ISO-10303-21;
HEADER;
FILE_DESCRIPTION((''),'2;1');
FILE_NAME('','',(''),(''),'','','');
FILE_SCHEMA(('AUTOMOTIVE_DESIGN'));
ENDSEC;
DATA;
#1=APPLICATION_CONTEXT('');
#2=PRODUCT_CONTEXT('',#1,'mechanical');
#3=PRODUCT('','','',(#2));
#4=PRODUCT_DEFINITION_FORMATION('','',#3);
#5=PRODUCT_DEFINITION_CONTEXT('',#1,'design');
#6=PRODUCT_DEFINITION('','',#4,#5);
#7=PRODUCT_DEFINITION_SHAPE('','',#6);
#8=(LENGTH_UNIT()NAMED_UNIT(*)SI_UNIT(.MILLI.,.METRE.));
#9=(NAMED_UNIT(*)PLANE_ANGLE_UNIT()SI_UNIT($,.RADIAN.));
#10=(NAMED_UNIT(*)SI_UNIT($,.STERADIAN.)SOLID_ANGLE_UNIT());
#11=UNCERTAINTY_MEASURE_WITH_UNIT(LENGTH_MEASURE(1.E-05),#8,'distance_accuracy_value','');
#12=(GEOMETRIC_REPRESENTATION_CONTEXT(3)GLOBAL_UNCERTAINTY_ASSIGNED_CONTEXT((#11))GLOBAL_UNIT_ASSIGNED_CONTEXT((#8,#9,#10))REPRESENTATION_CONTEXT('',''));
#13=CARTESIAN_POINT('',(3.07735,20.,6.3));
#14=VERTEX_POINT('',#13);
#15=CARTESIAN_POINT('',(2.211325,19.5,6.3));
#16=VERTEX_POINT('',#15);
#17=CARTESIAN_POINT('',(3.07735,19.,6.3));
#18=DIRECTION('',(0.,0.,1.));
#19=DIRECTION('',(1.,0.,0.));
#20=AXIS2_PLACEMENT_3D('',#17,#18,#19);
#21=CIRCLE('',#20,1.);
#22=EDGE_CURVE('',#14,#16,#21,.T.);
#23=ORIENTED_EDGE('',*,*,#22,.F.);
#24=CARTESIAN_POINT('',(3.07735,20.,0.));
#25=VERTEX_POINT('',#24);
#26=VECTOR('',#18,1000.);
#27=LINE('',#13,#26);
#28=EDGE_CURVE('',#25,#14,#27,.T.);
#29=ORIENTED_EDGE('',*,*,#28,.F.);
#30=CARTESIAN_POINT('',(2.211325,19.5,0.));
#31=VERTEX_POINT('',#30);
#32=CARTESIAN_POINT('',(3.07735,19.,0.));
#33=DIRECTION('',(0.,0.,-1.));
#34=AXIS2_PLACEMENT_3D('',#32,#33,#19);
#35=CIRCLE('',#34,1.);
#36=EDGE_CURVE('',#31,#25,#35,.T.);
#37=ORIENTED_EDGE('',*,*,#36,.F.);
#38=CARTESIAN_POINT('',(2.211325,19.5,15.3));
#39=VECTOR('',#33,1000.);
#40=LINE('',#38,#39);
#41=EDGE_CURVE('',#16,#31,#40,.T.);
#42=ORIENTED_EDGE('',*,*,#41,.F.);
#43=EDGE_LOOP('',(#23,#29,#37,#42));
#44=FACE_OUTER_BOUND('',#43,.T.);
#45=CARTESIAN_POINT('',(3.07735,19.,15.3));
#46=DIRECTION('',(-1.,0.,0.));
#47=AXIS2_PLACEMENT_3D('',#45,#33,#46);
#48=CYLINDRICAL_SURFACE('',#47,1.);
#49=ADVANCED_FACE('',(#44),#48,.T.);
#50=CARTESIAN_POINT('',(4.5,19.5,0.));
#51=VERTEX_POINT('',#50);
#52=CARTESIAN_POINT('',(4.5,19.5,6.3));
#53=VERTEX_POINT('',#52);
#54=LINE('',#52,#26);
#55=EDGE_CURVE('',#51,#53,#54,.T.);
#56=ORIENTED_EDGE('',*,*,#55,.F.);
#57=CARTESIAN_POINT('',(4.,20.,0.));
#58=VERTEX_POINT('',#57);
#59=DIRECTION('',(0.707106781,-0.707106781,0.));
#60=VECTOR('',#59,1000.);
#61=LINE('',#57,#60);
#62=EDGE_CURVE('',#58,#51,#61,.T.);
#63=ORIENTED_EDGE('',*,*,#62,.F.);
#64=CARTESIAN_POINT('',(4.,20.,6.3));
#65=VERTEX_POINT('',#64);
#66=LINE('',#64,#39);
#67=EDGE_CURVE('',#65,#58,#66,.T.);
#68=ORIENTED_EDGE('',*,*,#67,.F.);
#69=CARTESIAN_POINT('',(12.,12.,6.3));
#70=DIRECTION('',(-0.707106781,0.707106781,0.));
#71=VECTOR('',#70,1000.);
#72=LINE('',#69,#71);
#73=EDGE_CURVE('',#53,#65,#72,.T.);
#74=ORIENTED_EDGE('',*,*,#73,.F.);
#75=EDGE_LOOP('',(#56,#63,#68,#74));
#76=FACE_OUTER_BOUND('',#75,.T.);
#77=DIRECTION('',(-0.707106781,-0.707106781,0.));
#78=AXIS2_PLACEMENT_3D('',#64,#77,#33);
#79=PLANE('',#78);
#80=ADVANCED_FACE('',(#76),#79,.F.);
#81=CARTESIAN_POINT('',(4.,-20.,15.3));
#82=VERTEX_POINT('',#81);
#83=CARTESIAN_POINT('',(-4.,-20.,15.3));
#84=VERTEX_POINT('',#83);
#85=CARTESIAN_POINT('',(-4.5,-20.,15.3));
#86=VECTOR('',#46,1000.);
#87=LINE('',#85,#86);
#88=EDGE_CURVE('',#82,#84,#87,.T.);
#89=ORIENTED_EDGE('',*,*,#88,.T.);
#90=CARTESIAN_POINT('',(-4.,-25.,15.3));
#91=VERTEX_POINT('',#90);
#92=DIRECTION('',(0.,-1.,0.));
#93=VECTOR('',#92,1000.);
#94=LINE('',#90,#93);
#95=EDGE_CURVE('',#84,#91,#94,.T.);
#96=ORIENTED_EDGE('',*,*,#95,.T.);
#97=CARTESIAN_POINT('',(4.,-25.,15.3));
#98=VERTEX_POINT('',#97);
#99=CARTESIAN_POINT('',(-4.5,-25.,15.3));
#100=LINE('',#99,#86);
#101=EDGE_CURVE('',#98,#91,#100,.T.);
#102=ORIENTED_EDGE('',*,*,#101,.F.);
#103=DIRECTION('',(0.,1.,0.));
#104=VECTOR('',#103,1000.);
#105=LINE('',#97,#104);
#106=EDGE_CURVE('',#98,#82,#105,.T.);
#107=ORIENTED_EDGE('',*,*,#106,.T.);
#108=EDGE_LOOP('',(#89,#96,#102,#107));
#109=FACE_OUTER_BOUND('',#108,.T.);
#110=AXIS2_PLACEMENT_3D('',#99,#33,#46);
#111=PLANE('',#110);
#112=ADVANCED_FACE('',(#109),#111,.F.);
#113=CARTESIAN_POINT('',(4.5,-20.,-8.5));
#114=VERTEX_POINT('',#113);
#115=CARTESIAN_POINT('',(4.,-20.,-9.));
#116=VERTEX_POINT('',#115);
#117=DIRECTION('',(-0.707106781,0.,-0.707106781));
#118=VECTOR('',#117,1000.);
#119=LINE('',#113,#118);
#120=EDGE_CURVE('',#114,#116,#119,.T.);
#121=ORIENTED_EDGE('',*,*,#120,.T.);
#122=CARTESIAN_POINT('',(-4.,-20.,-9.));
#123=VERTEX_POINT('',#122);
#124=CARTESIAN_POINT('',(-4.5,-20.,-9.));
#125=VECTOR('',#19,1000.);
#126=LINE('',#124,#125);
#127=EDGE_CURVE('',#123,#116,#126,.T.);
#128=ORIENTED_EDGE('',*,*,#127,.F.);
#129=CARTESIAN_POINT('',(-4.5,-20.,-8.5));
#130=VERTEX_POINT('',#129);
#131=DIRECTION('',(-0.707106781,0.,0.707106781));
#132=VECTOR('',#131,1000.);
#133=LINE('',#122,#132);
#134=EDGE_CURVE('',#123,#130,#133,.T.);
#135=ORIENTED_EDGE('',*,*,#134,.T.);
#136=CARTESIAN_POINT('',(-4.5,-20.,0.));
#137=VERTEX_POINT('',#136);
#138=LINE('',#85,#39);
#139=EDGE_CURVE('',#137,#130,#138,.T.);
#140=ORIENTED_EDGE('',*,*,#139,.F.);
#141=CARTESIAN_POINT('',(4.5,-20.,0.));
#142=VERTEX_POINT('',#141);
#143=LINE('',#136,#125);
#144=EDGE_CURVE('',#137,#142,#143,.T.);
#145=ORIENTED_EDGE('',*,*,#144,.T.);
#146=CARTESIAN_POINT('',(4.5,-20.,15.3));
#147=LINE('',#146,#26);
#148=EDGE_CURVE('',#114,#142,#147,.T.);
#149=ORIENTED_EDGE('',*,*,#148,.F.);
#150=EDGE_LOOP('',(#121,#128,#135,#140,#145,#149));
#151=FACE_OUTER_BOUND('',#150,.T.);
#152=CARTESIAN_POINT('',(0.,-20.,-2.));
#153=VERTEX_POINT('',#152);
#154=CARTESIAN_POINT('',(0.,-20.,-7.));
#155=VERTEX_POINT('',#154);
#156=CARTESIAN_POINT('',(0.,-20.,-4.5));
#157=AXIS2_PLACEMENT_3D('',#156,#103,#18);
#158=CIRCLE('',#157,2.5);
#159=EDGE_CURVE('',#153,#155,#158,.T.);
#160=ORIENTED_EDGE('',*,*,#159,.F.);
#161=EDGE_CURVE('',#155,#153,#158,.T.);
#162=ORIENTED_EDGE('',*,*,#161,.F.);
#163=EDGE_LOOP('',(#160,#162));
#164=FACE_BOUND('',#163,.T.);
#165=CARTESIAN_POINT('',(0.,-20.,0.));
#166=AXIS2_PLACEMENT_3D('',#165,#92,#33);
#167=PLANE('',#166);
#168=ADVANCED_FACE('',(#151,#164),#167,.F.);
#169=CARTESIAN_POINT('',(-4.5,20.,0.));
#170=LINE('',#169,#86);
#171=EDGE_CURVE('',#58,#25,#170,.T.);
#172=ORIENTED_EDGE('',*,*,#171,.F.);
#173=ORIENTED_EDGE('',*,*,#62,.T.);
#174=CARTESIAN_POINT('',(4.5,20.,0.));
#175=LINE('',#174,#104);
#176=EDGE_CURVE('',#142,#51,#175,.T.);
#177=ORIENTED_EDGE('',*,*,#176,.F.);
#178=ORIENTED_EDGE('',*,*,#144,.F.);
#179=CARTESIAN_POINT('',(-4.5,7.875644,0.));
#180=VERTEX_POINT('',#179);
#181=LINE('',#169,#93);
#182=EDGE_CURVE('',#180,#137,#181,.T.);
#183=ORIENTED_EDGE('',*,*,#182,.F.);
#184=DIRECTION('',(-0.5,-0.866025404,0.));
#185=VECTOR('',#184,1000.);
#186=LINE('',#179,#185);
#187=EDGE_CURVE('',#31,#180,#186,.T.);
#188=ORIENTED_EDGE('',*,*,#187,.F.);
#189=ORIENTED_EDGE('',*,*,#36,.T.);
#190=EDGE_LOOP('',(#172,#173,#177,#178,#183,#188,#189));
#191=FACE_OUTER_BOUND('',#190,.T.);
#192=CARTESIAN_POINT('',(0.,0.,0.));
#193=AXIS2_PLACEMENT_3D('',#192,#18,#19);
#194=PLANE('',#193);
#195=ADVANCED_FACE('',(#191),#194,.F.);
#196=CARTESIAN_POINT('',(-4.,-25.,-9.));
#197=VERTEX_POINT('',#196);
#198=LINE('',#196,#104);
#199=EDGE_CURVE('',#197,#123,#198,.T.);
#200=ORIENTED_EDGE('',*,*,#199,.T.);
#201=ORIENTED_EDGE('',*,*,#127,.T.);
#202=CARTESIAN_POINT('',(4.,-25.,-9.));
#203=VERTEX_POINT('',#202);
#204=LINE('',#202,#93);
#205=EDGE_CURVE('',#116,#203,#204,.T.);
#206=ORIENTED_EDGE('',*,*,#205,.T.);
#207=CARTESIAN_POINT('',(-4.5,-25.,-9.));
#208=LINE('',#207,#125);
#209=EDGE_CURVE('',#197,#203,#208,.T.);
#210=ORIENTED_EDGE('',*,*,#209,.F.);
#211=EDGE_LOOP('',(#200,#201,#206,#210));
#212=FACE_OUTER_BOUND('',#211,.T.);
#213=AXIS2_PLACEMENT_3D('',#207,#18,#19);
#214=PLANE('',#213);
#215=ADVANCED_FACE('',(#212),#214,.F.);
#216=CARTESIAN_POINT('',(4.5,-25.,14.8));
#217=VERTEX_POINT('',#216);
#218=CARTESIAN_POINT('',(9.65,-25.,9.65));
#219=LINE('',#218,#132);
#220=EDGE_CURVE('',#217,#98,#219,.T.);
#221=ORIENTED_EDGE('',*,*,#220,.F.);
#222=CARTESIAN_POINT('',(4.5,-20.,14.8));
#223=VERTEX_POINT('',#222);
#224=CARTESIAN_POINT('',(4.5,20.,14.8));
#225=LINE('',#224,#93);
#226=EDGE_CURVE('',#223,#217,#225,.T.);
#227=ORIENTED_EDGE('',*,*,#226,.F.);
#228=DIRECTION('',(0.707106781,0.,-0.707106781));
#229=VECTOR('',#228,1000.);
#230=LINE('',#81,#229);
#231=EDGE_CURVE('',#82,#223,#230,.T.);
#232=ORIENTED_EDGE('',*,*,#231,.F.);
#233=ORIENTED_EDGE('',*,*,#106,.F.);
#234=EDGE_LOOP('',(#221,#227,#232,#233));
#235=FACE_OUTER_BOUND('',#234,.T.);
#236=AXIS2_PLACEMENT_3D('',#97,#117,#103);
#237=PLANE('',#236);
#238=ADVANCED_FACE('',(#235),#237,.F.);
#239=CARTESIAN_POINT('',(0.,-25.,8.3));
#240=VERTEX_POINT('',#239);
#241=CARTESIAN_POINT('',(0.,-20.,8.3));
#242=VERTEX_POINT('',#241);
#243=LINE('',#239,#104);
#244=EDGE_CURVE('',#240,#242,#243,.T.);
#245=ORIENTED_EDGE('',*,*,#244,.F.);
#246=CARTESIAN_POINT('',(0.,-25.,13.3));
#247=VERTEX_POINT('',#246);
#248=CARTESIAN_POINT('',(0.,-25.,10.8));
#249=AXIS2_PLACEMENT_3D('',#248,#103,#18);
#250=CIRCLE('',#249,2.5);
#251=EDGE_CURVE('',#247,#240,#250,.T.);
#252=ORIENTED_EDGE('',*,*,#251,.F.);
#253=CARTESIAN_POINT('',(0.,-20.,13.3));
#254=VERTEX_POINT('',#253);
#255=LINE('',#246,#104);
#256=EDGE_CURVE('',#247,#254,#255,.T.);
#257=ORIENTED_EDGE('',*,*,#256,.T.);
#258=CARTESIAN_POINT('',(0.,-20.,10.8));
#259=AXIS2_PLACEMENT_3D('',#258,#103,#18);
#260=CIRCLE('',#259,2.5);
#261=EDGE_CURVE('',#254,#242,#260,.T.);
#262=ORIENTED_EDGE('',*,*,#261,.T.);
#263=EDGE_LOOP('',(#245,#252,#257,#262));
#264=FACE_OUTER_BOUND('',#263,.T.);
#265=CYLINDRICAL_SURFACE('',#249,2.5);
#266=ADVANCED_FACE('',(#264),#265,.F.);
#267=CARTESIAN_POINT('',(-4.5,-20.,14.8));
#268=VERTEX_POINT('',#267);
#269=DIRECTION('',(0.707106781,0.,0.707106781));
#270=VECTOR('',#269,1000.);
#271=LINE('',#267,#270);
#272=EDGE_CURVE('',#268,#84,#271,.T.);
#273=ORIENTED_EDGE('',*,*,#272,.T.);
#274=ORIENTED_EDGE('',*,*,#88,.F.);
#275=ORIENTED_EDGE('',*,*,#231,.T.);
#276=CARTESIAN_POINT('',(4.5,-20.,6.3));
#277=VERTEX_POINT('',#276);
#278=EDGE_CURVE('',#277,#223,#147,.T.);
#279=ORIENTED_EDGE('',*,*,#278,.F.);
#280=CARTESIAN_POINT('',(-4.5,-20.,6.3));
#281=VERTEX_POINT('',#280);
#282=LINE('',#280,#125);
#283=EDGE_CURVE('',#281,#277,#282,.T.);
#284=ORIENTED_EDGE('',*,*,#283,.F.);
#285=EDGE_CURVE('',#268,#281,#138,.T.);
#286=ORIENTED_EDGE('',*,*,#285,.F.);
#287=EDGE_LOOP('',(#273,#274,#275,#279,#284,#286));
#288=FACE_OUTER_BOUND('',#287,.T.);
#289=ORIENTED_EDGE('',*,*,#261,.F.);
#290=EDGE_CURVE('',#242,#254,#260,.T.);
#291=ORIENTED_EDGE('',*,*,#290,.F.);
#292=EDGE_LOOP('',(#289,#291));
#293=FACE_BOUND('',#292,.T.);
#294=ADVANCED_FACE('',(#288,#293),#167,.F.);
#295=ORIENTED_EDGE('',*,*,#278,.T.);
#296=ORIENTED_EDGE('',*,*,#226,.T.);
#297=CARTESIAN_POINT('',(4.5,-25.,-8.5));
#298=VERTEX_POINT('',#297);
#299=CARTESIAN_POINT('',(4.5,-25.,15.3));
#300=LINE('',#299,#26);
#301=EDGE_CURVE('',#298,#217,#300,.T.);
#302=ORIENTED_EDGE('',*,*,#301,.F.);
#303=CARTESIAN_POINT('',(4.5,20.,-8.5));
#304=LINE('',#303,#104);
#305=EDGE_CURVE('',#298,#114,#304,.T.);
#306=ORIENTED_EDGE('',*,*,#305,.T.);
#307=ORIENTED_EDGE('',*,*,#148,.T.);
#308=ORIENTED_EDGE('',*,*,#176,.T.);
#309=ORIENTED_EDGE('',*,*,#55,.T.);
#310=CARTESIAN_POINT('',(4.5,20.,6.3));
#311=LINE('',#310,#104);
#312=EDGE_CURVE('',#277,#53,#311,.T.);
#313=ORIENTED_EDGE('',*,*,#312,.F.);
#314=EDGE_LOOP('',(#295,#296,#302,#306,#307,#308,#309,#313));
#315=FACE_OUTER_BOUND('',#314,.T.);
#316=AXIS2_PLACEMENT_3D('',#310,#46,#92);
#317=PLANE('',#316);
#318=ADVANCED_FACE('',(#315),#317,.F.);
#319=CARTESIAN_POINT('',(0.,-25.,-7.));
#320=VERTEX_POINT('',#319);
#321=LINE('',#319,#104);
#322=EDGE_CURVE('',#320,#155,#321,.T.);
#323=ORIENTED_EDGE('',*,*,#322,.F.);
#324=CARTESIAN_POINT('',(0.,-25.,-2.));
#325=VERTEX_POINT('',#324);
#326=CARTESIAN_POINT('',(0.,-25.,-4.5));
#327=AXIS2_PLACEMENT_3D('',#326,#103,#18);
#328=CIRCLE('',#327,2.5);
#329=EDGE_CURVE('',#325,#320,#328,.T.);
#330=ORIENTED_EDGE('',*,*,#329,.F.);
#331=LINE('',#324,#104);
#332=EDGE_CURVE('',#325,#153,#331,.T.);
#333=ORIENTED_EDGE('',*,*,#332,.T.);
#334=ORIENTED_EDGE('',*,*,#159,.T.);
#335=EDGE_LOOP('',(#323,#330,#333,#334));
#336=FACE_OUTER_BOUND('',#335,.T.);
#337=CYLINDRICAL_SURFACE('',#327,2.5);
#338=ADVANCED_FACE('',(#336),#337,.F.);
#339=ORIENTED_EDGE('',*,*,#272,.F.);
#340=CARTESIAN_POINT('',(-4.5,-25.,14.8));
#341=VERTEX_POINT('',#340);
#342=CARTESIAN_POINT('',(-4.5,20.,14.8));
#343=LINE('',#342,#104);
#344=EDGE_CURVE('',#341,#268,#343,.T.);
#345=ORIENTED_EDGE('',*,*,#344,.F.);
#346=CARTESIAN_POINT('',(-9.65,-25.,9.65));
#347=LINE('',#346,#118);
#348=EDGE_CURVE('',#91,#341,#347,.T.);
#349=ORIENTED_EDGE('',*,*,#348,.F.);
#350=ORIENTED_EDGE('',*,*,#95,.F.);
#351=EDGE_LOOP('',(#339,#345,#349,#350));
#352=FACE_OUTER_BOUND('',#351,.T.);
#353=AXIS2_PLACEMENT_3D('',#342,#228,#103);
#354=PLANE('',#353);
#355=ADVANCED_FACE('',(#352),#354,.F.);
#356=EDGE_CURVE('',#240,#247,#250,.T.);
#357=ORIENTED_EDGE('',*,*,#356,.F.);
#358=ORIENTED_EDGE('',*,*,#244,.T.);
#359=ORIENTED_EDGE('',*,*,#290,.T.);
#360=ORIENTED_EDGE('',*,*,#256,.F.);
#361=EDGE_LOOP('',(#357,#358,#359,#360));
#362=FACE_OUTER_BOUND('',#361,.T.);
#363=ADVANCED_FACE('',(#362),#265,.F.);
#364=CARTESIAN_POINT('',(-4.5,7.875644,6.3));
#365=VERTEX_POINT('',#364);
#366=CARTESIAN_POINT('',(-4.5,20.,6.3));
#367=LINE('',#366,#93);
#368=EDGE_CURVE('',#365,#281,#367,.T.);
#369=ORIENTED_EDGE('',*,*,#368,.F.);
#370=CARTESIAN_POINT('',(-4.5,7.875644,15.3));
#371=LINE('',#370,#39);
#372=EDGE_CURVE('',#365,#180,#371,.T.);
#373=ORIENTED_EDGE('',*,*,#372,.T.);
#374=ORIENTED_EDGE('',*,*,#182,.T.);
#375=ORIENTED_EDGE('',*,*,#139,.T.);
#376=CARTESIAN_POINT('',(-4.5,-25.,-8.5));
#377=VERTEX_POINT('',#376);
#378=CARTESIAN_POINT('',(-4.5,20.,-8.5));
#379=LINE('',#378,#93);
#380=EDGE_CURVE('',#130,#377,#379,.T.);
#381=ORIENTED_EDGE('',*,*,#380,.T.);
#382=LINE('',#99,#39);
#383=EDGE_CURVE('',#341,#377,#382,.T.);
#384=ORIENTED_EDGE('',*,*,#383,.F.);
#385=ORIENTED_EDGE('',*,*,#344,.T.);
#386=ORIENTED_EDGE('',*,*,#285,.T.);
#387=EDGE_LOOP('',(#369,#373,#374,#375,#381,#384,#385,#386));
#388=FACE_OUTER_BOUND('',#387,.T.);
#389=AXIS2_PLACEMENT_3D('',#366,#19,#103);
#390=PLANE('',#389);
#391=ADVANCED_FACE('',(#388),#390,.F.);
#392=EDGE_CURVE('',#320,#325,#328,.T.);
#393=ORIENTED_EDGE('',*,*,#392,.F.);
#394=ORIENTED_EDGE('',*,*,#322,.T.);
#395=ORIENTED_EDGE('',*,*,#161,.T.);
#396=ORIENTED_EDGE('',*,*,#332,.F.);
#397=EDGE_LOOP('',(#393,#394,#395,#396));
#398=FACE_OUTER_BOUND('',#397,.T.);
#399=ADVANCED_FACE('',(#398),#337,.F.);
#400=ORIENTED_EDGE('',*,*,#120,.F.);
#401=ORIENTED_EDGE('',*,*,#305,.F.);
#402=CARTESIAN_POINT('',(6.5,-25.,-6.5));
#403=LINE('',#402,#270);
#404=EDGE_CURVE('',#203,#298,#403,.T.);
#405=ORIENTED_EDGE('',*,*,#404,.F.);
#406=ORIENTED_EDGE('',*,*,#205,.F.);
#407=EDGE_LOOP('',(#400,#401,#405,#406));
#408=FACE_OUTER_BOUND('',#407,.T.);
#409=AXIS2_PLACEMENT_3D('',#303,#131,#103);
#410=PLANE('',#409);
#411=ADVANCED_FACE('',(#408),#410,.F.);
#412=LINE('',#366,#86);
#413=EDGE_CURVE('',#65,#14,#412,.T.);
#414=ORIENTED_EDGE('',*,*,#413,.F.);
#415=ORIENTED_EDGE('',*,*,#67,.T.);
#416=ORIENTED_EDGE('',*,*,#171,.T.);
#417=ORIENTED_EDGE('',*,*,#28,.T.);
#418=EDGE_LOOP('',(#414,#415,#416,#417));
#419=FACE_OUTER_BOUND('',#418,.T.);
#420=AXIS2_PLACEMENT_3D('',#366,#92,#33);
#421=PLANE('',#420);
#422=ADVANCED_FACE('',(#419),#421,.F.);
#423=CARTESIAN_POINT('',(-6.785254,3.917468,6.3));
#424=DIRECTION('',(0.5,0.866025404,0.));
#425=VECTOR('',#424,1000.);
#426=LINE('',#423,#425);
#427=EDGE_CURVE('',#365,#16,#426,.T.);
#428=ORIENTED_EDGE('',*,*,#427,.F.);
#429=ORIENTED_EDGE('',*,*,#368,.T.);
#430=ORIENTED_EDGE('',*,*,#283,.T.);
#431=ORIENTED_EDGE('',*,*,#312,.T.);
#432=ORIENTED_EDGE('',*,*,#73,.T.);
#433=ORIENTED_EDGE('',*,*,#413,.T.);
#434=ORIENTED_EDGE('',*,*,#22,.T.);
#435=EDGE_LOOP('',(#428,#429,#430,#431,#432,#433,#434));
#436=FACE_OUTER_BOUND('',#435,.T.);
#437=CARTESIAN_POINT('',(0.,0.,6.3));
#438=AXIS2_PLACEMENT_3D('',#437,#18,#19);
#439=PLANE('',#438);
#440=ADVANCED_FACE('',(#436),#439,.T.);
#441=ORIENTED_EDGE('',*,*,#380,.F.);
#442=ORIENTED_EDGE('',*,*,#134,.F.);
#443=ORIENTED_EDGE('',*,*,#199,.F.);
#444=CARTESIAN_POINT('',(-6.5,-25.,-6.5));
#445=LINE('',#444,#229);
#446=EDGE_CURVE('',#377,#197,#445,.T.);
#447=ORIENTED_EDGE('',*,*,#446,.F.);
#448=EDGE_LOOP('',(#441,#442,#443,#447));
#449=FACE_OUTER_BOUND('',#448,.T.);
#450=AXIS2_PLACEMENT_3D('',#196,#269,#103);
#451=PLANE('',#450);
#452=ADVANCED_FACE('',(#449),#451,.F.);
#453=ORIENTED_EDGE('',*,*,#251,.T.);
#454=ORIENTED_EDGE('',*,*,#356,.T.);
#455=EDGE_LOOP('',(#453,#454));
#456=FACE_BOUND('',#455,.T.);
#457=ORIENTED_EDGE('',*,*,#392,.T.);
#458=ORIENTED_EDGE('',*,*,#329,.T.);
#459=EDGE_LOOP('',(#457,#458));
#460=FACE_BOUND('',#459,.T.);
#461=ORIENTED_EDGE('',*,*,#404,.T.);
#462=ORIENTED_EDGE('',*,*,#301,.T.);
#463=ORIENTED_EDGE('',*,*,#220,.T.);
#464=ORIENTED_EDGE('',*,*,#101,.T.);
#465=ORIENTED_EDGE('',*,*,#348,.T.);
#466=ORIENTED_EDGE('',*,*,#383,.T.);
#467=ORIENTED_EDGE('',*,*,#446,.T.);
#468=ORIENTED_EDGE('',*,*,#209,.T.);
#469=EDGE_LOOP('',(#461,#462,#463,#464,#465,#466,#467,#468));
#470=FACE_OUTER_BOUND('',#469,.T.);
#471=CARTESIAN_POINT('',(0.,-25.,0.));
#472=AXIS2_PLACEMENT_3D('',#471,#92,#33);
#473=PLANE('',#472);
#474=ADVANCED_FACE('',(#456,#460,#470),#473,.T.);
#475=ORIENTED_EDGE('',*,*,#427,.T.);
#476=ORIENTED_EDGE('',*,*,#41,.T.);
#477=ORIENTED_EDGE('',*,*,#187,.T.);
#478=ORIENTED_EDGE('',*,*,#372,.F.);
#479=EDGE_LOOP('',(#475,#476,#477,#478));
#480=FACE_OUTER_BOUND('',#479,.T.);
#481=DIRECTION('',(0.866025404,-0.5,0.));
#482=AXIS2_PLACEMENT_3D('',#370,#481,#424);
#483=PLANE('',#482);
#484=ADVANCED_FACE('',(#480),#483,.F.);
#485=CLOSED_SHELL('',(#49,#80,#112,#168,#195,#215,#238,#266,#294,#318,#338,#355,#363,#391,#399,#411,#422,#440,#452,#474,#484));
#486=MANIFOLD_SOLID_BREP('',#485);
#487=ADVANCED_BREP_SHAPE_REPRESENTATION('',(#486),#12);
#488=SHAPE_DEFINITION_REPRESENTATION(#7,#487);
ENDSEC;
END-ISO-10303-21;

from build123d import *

# Parameters (mm, degrees)
SKETCH_1_W          = 9
SKETCH_1_H          = 40
EXTRUDE_1_DEPTH     = 6.3
SKETCH_2_W          = 9
SKETCH_2_H          = 24.3
EXTRUDE_2_DEPTH     = 5
CUT_EXTRUDE_1_DEPTH = 30.653667564
SKETCH_4_R          = 2.5
CUT_EXTRUDE_2_DEPTH = 44.062048256
FILLET_1_R          = 1
CHAMFER_2_SIZE      = 0.5


with BuildPart() as part:
    # 草图1 → 凸台-拉伸1 (new body)
    with BuildSketch(Plane.XY):
        Rectangle(SKETCH_1_W, SKETCH_1_H)
    extrude(amount=EXTRUDE_1_DEPTH)

    # 草图2 → 凸台-拉伸2 (add)
    with BuildSketch(Plane.XZ.offset(20)):
        with Locations((0, 3.15)):
            Rectangle(SKETCH_2_W, SKETCH_2_H)
    extrude(amount=EXTRUDE_2_DEPTH)

    # 草图3 → 切除-拉伸1 (cut, through all)
    with BuildSketch(Plane(origin=(0, 0, 0), x_dir=(-1, 0, 0), z_dir=(0, 0, -1))):
        Polygon((-2.5, 20), (4.5, 20), (4.5, 7.875644347), align=None)
    extrude(amount=-CUT_EXTRUDE_1_DEPTH, mode=Mode.SUBTRACT)

    # 草图4 → 切除-拉伸2 (cut, through all)
    with BuildSketch(Plane(origin=(0, -20, 0), x_dir=(1, 0, 0), z_dir=(0, 1, 0))):
        with Locations(Location((0, 4.5, 0), (0, 0, 270))):
            Circle(SKETCH_4_R)
        with Locations(Location((0, -10.8, 0), (0, 0, 270))):
            Circle(SKETCH_4_R)
    extrude(amount=-CUT_EXTRUDE_2_DEPTH, mode=Mode.SUBTRACT)

    # 圆角1
    fillet_1_edges = [part.edges().sort_by_distance(p)[0] for p in [
        (2.5, 20, 3.15),
    ]]
    fillet(fillet_1_edges, radius=FILLET_1_R)

    # 倒角2
    chamfer_2_edges = [part.edges().sort_by_distance(p)[0] for p in [
        (-4.5, -22.5, 15.3),
        (-4.5, -22.5, -9),
        (4.5, -22.5, -9),
        (4.5, -22.5, 15.3),
        (4.5, 20, 3.15),
    ]]
    chamfer(chamfer_2_edges, length=CHAMFER_2_SIZE)


solid = part.part
